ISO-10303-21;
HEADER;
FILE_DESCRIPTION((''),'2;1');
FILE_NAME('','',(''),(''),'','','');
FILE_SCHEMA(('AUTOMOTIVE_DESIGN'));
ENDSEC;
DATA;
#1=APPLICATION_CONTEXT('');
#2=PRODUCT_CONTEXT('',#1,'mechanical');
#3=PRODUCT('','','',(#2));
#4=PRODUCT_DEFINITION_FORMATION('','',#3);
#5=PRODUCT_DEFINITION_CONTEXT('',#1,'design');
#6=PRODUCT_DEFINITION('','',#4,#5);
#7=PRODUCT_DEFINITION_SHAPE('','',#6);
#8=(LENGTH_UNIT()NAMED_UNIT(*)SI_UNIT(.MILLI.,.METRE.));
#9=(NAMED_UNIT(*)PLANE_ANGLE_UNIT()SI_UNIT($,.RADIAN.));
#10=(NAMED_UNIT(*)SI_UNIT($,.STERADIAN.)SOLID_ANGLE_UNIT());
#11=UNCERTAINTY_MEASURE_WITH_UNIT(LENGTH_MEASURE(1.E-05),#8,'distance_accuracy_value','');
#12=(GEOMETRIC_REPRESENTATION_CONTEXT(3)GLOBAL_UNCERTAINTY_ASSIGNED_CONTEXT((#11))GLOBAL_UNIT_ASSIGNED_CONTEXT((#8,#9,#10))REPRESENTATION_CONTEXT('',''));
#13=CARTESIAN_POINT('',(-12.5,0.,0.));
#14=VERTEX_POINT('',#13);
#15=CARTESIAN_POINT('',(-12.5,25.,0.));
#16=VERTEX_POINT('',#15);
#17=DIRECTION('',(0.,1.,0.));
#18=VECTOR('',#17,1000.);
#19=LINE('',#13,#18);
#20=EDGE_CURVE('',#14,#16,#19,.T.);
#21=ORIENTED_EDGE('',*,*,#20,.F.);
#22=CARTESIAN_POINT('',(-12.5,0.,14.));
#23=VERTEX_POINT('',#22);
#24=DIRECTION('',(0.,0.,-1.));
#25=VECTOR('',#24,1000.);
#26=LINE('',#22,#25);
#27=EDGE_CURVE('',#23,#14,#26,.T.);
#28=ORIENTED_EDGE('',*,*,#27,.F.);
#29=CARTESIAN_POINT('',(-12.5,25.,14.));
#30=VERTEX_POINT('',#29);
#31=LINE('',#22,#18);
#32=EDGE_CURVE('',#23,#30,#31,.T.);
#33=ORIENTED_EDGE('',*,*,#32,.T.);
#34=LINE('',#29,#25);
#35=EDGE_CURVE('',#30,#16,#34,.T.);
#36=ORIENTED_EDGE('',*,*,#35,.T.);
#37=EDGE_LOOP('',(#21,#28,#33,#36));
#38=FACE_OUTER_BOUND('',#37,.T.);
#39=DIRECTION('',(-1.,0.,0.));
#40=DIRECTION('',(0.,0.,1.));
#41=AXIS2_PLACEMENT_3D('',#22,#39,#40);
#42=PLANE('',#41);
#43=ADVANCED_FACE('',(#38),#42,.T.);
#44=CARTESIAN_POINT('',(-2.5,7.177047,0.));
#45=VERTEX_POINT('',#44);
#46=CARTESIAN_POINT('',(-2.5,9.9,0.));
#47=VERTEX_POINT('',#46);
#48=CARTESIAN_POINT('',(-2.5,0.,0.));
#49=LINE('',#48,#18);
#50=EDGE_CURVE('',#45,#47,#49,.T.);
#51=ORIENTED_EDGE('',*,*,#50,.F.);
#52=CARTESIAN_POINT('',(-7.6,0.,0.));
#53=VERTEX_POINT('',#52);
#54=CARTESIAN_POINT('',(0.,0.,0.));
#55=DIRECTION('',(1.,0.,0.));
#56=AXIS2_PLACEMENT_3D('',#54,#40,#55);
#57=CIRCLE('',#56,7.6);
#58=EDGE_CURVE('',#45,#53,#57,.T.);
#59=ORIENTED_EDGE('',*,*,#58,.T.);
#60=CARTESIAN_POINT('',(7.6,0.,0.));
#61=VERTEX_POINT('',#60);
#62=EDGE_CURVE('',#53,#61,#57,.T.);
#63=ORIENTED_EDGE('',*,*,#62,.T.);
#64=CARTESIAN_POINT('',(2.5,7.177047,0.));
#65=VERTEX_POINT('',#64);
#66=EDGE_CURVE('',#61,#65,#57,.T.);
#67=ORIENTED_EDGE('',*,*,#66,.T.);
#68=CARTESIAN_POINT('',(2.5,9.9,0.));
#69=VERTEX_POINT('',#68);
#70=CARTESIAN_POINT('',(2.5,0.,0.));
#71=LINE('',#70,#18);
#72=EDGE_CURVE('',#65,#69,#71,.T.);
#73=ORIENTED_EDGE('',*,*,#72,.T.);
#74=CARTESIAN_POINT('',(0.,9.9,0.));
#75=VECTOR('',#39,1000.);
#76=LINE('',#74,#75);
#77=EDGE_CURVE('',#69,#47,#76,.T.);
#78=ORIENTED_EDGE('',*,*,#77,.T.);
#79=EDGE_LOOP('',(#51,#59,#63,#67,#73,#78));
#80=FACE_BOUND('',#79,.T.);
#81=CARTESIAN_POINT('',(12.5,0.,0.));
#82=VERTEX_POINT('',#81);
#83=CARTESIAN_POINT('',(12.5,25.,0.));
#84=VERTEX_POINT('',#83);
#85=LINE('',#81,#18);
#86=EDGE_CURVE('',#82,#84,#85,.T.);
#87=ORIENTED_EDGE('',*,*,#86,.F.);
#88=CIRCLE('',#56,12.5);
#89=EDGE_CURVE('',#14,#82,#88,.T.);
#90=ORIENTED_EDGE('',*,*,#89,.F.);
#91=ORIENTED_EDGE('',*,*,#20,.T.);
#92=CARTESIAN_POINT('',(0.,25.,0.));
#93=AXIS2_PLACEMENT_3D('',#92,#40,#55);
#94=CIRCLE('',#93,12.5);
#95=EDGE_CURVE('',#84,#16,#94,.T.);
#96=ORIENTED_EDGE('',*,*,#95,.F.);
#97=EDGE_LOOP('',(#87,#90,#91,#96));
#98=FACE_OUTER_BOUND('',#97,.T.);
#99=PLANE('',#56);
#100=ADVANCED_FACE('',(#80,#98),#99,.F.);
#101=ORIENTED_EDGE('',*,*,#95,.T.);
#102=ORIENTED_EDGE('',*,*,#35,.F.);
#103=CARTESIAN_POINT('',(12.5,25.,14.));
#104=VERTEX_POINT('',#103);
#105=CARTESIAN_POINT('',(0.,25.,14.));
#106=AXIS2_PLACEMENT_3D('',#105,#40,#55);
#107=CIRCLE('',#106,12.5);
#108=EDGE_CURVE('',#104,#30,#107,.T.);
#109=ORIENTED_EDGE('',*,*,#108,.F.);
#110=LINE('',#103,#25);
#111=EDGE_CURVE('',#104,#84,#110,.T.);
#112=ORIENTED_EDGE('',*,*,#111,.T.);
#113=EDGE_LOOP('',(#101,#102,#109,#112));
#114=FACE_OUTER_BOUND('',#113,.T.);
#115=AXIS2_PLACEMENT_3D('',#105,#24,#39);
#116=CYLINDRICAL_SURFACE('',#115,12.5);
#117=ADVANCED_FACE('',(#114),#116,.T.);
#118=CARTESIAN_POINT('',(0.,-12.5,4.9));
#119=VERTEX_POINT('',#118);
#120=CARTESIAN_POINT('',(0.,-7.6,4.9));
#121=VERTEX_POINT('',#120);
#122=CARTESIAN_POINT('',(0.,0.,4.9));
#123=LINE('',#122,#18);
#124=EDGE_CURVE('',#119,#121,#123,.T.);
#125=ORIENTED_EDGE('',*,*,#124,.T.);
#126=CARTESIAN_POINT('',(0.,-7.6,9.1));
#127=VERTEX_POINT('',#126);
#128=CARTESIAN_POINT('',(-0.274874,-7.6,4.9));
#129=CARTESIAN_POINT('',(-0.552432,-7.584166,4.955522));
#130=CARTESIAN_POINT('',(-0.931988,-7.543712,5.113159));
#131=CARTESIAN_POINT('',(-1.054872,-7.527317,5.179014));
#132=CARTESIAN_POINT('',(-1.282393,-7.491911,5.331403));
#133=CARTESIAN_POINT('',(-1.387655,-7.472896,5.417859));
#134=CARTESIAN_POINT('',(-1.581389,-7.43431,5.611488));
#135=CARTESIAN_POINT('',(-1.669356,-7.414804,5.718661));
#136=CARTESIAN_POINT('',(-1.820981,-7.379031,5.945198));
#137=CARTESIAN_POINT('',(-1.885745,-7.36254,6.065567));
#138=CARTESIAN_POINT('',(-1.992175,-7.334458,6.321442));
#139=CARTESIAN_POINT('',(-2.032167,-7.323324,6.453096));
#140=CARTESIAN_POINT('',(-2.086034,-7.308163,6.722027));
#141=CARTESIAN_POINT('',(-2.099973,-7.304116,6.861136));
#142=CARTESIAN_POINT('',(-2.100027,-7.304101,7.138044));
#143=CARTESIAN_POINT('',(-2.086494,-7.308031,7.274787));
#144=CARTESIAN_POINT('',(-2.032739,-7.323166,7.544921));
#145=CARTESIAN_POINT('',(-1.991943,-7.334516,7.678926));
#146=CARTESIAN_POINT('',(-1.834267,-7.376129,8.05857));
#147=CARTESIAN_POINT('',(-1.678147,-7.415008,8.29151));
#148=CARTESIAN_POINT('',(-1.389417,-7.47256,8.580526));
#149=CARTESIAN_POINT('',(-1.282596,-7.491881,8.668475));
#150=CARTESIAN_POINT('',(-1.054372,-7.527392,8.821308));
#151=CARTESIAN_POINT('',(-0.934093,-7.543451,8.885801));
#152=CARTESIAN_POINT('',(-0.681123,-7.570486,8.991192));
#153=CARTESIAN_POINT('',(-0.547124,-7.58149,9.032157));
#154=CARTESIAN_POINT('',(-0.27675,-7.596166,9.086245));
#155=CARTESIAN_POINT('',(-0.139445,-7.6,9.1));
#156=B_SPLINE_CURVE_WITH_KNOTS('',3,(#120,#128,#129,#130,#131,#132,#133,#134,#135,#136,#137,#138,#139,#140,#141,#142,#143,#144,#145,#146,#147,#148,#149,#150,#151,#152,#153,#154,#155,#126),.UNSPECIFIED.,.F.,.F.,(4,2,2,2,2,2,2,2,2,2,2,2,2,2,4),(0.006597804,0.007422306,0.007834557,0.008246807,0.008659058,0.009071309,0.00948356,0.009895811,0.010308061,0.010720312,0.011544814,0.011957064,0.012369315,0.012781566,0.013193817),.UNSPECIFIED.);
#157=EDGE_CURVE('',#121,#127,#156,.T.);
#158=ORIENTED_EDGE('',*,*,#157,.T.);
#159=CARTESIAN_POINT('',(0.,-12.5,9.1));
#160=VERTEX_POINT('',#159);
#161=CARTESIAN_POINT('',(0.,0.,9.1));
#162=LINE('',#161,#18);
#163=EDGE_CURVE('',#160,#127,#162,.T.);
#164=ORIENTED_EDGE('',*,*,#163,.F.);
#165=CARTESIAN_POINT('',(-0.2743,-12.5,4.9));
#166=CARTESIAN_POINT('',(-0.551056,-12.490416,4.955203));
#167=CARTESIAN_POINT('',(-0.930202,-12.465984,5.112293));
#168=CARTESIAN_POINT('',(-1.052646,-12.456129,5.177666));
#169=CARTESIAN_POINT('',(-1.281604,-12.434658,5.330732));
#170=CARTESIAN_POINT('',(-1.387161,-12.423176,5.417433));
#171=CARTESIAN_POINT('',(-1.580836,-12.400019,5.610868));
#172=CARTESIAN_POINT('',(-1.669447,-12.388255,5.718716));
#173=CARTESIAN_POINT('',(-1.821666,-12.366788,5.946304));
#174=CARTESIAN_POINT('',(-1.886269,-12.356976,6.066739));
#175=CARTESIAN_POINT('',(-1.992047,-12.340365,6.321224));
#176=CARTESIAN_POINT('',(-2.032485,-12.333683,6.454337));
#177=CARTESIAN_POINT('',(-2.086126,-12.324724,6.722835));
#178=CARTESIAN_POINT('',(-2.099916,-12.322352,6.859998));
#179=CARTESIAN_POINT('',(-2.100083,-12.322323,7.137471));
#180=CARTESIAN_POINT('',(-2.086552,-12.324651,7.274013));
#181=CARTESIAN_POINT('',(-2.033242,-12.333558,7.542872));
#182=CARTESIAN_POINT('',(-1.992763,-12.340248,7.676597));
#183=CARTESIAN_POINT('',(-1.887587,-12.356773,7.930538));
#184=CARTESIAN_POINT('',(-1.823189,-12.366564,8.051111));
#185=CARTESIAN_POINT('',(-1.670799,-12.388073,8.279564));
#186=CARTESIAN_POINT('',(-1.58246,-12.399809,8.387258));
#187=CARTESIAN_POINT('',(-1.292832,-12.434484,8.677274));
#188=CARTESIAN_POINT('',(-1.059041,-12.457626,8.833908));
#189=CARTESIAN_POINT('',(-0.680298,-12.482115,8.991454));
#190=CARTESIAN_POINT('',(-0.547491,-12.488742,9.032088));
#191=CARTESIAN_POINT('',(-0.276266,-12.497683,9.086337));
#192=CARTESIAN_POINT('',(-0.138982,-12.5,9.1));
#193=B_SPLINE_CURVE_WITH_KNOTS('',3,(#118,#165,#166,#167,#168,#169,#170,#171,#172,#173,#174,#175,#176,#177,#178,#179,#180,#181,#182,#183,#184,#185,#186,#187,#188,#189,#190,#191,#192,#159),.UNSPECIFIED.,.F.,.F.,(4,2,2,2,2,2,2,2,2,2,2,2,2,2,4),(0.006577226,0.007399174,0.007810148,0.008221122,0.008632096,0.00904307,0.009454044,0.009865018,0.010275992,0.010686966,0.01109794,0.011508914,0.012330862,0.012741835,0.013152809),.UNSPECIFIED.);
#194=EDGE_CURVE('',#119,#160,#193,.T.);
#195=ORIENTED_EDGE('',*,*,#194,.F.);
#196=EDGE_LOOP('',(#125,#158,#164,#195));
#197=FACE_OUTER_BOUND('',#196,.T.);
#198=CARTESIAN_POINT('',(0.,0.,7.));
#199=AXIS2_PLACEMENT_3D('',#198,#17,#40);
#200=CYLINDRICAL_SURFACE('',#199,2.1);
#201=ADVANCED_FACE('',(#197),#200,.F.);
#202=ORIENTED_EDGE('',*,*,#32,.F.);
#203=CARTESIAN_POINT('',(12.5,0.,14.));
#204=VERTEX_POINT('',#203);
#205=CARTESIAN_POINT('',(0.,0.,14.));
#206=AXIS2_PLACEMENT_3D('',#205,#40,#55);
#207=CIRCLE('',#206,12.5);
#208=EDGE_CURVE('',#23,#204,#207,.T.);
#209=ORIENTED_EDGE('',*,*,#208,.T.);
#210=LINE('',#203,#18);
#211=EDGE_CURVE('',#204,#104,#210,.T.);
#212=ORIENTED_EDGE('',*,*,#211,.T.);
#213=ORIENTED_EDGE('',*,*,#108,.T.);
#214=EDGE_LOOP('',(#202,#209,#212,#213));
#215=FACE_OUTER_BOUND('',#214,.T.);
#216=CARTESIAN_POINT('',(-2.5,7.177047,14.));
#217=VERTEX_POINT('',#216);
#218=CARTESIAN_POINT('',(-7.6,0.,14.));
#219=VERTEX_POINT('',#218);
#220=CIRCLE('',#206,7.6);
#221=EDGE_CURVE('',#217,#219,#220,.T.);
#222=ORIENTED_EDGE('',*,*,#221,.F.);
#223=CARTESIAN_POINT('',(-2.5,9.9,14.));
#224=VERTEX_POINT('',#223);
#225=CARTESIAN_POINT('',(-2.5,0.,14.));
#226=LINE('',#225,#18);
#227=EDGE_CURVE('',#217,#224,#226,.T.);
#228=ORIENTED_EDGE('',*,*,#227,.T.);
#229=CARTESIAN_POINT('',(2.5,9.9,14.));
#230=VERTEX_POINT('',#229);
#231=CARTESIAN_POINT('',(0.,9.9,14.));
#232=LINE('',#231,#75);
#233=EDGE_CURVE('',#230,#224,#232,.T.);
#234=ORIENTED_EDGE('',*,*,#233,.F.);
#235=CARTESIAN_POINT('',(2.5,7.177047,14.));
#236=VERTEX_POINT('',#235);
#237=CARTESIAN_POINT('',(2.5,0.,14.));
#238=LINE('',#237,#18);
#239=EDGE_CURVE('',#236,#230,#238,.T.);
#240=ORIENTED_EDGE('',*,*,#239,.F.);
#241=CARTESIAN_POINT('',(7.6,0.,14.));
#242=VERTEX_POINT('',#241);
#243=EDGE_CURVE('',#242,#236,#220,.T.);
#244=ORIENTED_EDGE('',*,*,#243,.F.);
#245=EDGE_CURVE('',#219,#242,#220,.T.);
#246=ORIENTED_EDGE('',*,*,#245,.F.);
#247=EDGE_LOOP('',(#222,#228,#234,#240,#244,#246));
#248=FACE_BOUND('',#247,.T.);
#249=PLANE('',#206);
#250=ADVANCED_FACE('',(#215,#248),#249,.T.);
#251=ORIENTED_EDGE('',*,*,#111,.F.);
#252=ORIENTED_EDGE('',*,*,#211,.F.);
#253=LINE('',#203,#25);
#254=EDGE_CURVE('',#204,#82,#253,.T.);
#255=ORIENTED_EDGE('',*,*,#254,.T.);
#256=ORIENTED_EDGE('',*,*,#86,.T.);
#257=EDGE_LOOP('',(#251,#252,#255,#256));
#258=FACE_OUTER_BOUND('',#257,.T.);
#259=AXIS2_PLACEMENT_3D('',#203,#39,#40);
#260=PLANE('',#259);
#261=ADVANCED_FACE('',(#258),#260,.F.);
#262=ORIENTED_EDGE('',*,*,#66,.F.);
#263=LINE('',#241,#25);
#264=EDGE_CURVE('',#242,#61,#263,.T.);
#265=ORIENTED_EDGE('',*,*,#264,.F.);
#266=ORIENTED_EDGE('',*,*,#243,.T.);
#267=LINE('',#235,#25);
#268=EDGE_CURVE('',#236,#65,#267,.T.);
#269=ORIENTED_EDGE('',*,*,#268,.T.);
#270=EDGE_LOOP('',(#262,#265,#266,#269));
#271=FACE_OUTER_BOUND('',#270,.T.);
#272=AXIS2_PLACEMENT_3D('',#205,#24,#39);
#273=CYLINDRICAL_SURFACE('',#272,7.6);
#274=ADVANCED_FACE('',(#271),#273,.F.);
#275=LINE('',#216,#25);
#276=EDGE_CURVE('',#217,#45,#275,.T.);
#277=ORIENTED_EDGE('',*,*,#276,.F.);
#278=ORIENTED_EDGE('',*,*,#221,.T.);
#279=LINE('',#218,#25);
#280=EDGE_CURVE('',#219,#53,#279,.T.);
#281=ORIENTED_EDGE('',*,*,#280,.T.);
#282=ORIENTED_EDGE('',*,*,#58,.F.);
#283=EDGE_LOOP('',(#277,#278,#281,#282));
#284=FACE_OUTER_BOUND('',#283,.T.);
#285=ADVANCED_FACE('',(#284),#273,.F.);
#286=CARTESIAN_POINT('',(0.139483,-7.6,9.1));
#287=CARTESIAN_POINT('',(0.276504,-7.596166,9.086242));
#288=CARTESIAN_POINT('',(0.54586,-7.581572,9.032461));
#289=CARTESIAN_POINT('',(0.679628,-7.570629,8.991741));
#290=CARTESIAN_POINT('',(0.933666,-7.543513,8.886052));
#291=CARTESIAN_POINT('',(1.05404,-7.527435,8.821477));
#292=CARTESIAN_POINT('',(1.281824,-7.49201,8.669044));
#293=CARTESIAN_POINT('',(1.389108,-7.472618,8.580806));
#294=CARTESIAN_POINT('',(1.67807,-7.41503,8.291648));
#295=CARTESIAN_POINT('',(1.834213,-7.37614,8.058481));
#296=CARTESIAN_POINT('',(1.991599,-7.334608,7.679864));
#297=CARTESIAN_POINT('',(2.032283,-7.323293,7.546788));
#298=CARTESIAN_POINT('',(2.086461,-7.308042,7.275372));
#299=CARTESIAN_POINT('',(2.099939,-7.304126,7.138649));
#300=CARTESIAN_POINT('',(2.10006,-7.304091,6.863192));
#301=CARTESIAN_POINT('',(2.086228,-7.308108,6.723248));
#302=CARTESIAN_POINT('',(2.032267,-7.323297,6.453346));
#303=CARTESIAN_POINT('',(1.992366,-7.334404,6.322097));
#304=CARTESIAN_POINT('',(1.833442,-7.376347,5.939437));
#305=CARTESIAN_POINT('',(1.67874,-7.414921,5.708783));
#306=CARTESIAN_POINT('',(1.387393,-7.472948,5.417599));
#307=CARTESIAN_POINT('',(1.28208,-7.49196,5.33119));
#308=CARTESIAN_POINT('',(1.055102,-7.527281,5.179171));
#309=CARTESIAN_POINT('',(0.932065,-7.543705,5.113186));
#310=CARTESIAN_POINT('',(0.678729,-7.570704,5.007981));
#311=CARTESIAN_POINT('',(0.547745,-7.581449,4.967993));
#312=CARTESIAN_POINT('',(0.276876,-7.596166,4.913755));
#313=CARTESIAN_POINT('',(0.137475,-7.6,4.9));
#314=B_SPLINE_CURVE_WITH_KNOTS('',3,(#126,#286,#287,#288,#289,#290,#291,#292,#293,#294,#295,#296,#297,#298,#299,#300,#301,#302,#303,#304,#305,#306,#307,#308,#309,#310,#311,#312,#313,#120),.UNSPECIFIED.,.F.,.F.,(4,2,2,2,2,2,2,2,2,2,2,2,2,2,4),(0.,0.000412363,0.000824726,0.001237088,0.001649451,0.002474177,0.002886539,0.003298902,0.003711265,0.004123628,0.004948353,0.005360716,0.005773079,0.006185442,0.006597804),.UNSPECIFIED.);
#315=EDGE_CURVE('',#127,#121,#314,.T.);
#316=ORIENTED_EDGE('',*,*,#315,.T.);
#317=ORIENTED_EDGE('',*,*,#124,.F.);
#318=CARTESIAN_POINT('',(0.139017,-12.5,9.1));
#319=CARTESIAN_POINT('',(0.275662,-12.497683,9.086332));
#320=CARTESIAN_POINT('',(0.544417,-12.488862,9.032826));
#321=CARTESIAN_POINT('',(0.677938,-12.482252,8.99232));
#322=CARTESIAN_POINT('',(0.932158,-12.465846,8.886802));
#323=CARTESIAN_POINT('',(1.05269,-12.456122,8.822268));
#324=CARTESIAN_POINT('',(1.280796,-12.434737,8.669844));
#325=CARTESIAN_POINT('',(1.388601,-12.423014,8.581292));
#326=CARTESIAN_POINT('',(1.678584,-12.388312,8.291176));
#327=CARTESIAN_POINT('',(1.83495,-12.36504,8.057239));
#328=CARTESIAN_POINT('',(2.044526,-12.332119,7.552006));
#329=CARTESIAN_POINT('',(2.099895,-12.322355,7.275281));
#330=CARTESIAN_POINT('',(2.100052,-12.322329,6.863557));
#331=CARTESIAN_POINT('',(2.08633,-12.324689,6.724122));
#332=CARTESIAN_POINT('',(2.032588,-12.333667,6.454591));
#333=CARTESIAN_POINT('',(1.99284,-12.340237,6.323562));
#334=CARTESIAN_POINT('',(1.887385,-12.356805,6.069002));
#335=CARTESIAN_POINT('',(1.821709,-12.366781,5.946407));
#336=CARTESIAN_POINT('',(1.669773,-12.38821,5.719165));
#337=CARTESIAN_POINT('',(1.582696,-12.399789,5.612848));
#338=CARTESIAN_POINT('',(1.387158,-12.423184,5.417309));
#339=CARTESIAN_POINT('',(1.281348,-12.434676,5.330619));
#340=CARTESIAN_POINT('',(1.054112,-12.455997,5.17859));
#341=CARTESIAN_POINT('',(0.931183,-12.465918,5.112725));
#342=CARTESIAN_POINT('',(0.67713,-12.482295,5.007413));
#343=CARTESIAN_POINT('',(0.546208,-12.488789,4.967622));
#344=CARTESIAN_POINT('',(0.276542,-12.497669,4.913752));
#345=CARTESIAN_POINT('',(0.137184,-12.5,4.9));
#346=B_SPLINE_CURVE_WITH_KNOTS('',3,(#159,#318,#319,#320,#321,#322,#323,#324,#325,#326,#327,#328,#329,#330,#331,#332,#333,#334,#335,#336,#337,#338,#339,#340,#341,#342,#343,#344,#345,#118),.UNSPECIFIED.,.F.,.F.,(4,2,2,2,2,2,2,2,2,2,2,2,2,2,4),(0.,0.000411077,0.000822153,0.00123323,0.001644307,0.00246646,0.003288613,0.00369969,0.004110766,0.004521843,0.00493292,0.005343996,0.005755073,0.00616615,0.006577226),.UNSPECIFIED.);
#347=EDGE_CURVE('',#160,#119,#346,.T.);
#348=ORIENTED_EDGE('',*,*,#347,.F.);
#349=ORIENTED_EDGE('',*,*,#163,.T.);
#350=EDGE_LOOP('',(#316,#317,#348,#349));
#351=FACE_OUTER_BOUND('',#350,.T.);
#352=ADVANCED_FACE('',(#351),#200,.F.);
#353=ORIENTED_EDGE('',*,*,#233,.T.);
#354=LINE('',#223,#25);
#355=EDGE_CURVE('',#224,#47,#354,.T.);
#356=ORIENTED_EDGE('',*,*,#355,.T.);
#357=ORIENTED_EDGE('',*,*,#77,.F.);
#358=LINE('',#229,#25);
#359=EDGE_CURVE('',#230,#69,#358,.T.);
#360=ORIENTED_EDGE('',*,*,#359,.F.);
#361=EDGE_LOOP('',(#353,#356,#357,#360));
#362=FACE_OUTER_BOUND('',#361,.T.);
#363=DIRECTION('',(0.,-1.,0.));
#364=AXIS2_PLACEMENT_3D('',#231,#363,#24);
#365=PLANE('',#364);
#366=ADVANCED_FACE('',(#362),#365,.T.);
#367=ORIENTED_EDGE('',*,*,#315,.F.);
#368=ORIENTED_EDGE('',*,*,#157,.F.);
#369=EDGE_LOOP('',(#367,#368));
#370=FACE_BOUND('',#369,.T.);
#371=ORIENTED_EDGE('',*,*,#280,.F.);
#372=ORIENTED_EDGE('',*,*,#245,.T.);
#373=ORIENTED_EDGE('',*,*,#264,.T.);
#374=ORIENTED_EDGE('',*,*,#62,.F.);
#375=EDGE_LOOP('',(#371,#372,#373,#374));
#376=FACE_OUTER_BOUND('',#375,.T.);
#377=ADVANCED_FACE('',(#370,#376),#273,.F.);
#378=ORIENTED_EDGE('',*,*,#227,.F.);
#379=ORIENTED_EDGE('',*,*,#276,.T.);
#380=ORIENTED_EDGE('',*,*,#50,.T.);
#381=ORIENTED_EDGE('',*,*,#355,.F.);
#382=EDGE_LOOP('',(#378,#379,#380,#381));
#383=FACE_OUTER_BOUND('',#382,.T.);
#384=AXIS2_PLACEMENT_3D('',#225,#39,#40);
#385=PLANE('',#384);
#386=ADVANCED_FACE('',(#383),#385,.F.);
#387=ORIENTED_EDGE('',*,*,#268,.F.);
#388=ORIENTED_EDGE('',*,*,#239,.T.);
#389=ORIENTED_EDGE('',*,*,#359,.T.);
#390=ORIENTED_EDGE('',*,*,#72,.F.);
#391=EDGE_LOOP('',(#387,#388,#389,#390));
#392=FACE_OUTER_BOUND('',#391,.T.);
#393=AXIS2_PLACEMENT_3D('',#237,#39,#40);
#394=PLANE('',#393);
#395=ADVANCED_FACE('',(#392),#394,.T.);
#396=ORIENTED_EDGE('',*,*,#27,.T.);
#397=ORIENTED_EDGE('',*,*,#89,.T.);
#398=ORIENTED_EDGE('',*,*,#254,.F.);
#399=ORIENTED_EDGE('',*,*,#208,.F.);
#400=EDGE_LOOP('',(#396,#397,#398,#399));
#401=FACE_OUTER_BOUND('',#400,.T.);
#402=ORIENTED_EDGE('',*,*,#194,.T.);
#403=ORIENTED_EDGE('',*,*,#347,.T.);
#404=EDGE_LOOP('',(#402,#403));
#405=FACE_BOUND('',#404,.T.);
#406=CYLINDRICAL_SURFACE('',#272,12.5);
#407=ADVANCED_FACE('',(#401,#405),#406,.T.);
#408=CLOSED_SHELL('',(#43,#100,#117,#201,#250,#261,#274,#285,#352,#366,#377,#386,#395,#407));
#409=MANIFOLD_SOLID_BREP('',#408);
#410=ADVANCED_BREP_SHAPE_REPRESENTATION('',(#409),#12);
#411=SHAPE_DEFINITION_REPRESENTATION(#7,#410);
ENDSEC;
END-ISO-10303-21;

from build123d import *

# Parameters (mm, degrees)
BOSS_EXTRUDE1_DEPTH = 14
SKETCH3_W           = 2.1
SKETCH3_H           = 12.5


with BuildPart() as part:
    # Sketch1 → Boss-Extrude1 (new body)
    with BuildSketch(Plane.XY):
        with BuildLine():
            Line((-12.5, 25), (-12.5, 0))
            ThreePointArc((-12.5, 0), (0, -12.5), (12.5, 0))
            Line((12.5, 0), (12.5, 25))
            ThreePointArc((12.5, 25), (0, 37.5), (-12.5, 25))
        make_face()
        with BuildLine():
            Line((2.5, 9.9), (2.5, 7.177046746))
            ThreePointArc((2.5, 7.177046746), (6.195159401, 4.402272141), (7.6, 0))
            ThreePointArc((7.6, 0), (-4.402272141, -6.195159401), (-2.5, 7.177046746))
            Line((-2.5, 7.177046746), (-2.5, 9.9))
            Line((-2.5, 9.9), (2.5, 9.9))
        make_face(mode=Mode.SUBTRACT)
    extrude(amount=BOSS_EXTRUDE1_DEPTH)

    # Sketch3 → M5 Tapped Hole1 (revolve, cut)
    with BuildSketch(Plane(origin=(0, 0, 7), x_dir=(0, 0, 1), z_dir=(1, 0, 0))):
        with Locations((1.05, 6.25)):
            Rectangle(SKETCH3_W, SKETCH3_H)
    revolve(axis=Axis((0, 6.35, 7), (0, -1, 0)), mode=Mode.SUBTRACT)


solid = part.part
